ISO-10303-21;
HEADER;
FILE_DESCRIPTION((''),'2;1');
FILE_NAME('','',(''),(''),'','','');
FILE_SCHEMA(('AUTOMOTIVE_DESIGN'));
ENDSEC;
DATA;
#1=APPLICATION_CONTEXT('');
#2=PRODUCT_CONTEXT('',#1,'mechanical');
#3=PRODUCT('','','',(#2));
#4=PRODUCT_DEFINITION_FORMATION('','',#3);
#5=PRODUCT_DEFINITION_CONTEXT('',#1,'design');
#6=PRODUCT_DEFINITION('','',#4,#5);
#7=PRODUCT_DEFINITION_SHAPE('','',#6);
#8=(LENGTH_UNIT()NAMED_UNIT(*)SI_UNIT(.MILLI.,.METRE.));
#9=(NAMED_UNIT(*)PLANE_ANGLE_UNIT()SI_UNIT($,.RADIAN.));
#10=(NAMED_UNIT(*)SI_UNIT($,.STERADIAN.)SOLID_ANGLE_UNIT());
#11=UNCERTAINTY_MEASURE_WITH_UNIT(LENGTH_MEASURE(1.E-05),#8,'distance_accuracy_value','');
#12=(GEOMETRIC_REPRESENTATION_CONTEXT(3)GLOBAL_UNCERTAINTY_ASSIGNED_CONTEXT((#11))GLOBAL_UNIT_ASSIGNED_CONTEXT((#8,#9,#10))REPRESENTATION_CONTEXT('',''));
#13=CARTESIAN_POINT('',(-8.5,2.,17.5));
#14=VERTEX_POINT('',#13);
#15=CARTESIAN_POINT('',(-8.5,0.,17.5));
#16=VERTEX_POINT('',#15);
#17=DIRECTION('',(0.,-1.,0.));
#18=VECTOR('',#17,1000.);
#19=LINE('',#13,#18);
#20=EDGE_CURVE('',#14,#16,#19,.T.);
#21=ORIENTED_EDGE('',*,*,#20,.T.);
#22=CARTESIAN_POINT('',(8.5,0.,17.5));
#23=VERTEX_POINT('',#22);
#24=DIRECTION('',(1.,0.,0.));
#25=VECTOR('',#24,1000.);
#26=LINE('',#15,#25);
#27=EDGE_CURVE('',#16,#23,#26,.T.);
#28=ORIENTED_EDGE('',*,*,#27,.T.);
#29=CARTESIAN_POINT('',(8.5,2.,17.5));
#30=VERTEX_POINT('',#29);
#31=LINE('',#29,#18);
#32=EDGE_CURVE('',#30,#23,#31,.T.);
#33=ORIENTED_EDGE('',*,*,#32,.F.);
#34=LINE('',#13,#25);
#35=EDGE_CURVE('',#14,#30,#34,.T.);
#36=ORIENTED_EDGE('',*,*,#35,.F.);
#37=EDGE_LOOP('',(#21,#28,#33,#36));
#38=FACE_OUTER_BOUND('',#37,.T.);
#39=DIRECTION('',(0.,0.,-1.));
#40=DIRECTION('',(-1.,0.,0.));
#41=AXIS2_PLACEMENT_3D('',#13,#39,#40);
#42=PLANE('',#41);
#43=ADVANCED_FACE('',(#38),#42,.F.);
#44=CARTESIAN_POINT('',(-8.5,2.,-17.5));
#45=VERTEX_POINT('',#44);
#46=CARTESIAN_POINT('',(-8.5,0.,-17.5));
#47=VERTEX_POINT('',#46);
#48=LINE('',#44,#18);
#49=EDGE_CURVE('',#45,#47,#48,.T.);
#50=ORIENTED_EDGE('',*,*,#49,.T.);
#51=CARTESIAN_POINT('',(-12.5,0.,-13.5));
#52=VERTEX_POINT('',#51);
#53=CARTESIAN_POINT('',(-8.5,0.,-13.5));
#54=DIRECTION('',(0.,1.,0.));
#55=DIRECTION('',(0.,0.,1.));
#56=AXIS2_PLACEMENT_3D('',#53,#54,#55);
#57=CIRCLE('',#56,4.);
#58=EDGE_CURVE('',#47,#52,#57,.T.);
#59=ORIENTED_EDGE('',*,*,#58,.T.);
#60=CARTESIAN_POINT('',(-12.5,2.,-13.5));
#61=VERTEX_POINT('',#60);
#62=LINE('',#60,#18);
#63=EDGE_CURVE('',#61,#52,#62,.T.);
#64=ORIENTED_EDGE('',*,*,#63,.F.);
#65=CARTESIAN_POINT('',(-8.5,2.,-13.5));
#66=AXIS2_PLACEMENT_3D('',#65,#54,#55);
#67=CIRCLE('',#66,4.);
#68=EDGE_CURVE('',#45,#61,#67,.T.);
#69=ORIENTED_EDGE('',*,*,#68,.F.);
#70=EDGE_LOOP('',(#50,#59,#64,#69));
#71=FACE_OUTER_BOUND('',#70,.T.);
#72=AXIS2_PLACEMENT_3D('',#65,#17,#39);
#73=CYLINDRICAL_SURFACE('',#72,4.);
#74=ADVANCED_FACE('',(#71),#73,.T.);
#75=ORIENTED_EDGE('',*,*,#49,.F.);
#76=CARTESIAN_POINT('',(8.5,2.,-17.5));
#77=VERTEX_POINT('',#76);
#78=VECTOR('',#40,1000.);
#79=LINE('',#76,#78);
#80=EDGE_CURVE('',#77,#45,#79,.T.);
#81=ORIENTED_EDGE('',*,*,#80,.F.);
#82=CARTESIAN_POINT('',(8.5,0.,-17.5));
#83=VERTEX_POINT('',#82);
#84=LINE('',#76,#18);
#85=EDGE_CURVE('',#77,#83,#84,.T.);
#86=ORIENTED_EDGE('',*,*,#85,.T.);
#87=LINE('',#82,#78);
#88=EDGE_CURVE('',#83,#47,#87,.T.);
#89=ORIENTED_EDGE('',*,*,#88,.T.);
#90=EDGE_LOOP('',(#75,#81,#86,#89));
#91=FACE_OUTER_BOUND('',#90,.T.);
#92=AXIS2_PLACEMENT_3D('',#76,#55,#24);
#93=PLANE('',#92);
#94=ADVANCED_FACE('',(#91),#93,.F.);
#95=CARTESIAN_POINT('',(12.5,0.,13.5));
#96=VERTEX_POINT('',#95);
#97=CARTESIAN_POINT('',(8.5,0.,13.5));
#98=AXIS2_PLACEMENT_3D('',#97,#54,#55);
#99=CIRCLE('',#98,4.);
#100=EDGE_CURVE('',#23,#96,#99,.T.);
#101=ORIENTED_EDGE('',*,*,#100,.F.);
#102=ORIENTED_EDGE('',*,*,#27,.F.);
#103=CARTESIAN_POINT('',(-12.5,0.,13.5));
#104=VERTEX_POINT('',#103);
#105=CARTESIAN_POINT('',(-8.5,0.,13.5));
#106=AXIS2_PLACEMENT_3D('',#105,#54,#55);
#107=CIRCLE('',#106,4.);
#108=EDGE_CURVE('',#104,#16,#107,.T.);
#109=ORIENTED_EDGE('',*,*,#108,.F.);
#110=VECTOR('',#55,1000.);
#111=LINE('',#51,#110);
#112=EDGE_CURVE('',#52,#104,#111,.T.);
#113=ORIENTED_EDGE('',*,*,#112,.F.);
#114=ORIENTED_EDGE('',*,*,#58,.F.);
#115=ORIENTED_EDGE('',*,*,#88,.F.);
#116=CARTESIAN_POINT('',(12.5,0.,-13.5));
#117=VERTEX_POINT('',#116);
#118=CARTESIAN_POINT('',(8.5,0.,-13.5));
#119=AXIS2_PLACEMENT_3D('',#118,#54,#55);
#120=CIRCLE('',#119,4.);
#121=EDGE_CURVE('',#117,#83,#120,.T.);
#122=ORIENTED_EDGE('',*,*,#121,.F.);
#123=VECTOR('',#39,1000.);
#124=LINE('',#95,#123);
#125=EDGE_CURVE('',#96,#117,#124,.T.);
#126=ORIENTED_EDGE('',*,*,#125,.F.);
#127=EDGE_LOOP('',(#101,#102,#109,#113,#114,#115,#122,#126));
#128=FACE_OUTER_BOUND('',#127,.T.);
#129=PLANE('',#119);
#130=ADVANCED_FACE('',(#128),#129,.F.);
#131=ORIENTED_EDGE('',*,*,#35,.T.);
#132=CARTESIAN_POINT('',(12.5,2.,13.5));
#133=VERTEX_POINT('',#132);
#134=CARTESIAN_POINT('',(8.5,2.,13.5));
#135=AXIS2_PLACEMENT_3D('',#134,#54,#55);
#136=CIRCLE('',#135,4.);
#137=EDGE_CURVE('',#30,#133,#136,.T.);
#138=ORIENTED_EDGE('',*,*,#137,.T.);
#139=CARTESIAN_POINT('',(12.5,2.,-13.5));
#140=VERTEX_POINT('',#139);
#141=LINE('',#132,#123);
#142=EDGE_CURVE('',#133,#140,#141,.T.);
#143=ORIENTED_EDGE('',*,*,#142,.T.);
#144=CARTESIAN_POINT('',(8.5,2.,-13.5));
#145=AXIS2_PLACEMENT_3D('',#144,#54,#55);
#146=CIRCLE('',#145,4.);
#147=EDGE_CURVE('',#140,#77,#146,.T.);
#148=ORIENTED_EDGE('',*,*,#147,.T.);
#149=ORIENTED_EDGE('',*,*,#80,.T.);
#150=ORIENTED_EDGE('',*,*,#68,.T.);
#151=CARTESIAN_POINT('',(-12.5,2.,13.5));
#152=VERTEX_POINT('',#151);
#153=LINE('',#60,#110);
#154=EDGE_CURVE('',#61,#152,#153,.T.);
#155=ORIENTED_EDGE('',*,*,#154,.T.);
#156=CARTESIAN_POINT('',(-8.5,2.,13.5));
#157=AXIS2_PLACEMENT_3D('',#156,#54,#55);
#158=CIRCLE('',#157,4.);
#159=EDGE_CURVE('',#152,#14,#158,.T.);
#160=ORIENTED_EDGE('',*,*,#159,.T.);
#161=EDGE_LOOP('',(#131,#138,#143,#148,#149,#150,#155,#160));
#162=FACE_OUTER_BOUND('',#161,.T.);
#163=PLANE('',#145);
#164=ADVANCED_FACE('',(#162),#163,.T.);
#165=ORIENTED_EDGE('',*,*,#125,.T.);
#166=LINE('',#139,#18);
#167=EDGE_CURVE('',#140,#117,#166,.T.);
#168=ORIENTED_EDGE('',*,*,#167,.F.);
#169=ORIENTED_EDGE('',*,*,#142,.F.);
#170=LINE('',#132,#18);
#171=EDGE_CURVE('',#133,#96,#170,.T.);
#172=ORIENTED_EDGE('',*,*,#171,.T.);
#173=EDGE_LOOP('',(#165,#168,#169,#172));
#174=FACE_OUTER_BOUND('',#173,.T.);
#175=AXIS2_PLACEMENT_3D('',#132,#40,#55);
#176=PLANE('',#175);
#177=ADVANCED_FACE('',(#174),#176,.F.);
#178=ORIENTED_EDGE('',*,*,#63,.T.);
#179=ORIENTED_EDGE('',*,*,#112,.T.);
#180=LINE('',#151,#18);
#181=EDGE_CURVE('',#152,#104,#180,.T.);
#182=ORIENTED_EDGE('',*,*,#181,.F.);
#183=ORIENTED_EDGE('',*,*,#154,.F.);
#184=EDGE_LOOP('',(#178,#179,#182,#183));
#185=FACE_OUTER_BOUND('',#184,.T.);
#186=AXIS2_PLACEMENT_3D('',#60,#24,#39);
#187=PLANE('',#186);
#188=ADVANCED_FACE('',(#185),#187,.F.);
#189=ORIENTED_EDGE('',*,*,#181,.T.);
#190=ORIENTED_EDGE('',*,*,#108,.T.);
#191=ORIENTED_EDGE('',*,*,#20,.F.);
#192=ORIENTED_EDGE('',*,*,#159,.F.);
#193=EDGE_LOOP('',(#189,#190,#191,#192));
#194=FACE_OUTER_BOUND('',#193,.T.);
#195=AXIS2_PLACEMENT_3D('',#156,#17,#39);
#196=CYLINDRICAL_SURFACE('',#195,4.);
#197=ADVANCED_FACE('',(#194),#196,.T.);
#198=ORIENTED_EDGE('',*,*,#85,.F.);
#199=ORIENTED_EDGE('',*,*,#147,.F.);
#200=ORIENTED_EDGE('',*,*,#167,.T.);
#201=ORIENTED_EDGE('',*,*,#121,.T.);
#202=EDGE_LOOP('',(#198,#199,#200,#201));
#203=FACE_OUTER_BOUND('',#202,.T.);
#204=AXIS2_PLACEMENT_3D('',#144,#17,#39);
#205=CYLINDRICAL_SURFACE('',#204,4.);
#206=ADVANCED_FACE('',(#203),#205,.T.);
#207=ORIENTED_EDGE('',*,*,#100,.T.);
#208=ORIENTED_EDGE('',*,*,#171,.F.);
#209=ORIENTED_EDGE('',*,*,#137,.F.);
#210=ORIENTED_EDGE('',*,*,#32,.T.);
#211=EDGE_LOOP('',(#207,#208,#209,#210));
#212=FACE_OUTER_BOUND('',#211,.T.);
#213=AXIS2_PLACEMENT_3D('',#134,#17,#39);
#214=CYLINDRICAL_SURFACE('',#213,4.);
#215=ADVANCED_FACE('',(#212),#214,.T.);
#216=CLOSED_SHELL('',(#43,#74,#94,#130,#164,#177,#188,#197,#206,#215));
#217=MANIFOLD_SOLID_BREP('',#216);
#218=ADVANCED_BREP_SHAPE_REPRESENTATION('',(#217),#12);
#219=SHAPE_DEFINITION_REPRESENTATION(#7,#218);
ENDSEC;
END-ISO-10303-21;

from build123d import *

# Parameters (mm, degrees)
BOSS_EXTRU_1_DEPTH = 2


with BuildPart() as part:
    # Sketch1 → Boss.-Extru.1 (new body)
    with BuildSketch(Plane(origin=(0, 0, 0), x_dir=(1, 0, 0), z_dir=(0, 1, 0))):
        with BuildLine():
            Line((8.5, 17.5), (-8.5, 17.5))
            ThreePointArc((-8.5, 17.5), (-11.328427125, 16.328427125), (-12.5, 13.5))
            Line((-12.5, 13.5), (-12.5, -13.5))
            ThreePointArc((-12.5, -13.5), (-11.328427125, -16.328427125), (-8.5, -17.5))
            Line((-8.5, -17.5), (8.5, -17.5))
            ThreePointArc((8.5, -17.5), (11.328427125, -16.328427125), (12.5, -13.5))
            Line((12.5, -13.5), (12.5, 13.5))
            ThreePointArc((12.5, 13.5), (11.328427125, 16.328427125), (8.5, 17.5))
        make_face()
    extrude(amount=BOSS_EXTRU_1_DEPTH)


solid = part.part
